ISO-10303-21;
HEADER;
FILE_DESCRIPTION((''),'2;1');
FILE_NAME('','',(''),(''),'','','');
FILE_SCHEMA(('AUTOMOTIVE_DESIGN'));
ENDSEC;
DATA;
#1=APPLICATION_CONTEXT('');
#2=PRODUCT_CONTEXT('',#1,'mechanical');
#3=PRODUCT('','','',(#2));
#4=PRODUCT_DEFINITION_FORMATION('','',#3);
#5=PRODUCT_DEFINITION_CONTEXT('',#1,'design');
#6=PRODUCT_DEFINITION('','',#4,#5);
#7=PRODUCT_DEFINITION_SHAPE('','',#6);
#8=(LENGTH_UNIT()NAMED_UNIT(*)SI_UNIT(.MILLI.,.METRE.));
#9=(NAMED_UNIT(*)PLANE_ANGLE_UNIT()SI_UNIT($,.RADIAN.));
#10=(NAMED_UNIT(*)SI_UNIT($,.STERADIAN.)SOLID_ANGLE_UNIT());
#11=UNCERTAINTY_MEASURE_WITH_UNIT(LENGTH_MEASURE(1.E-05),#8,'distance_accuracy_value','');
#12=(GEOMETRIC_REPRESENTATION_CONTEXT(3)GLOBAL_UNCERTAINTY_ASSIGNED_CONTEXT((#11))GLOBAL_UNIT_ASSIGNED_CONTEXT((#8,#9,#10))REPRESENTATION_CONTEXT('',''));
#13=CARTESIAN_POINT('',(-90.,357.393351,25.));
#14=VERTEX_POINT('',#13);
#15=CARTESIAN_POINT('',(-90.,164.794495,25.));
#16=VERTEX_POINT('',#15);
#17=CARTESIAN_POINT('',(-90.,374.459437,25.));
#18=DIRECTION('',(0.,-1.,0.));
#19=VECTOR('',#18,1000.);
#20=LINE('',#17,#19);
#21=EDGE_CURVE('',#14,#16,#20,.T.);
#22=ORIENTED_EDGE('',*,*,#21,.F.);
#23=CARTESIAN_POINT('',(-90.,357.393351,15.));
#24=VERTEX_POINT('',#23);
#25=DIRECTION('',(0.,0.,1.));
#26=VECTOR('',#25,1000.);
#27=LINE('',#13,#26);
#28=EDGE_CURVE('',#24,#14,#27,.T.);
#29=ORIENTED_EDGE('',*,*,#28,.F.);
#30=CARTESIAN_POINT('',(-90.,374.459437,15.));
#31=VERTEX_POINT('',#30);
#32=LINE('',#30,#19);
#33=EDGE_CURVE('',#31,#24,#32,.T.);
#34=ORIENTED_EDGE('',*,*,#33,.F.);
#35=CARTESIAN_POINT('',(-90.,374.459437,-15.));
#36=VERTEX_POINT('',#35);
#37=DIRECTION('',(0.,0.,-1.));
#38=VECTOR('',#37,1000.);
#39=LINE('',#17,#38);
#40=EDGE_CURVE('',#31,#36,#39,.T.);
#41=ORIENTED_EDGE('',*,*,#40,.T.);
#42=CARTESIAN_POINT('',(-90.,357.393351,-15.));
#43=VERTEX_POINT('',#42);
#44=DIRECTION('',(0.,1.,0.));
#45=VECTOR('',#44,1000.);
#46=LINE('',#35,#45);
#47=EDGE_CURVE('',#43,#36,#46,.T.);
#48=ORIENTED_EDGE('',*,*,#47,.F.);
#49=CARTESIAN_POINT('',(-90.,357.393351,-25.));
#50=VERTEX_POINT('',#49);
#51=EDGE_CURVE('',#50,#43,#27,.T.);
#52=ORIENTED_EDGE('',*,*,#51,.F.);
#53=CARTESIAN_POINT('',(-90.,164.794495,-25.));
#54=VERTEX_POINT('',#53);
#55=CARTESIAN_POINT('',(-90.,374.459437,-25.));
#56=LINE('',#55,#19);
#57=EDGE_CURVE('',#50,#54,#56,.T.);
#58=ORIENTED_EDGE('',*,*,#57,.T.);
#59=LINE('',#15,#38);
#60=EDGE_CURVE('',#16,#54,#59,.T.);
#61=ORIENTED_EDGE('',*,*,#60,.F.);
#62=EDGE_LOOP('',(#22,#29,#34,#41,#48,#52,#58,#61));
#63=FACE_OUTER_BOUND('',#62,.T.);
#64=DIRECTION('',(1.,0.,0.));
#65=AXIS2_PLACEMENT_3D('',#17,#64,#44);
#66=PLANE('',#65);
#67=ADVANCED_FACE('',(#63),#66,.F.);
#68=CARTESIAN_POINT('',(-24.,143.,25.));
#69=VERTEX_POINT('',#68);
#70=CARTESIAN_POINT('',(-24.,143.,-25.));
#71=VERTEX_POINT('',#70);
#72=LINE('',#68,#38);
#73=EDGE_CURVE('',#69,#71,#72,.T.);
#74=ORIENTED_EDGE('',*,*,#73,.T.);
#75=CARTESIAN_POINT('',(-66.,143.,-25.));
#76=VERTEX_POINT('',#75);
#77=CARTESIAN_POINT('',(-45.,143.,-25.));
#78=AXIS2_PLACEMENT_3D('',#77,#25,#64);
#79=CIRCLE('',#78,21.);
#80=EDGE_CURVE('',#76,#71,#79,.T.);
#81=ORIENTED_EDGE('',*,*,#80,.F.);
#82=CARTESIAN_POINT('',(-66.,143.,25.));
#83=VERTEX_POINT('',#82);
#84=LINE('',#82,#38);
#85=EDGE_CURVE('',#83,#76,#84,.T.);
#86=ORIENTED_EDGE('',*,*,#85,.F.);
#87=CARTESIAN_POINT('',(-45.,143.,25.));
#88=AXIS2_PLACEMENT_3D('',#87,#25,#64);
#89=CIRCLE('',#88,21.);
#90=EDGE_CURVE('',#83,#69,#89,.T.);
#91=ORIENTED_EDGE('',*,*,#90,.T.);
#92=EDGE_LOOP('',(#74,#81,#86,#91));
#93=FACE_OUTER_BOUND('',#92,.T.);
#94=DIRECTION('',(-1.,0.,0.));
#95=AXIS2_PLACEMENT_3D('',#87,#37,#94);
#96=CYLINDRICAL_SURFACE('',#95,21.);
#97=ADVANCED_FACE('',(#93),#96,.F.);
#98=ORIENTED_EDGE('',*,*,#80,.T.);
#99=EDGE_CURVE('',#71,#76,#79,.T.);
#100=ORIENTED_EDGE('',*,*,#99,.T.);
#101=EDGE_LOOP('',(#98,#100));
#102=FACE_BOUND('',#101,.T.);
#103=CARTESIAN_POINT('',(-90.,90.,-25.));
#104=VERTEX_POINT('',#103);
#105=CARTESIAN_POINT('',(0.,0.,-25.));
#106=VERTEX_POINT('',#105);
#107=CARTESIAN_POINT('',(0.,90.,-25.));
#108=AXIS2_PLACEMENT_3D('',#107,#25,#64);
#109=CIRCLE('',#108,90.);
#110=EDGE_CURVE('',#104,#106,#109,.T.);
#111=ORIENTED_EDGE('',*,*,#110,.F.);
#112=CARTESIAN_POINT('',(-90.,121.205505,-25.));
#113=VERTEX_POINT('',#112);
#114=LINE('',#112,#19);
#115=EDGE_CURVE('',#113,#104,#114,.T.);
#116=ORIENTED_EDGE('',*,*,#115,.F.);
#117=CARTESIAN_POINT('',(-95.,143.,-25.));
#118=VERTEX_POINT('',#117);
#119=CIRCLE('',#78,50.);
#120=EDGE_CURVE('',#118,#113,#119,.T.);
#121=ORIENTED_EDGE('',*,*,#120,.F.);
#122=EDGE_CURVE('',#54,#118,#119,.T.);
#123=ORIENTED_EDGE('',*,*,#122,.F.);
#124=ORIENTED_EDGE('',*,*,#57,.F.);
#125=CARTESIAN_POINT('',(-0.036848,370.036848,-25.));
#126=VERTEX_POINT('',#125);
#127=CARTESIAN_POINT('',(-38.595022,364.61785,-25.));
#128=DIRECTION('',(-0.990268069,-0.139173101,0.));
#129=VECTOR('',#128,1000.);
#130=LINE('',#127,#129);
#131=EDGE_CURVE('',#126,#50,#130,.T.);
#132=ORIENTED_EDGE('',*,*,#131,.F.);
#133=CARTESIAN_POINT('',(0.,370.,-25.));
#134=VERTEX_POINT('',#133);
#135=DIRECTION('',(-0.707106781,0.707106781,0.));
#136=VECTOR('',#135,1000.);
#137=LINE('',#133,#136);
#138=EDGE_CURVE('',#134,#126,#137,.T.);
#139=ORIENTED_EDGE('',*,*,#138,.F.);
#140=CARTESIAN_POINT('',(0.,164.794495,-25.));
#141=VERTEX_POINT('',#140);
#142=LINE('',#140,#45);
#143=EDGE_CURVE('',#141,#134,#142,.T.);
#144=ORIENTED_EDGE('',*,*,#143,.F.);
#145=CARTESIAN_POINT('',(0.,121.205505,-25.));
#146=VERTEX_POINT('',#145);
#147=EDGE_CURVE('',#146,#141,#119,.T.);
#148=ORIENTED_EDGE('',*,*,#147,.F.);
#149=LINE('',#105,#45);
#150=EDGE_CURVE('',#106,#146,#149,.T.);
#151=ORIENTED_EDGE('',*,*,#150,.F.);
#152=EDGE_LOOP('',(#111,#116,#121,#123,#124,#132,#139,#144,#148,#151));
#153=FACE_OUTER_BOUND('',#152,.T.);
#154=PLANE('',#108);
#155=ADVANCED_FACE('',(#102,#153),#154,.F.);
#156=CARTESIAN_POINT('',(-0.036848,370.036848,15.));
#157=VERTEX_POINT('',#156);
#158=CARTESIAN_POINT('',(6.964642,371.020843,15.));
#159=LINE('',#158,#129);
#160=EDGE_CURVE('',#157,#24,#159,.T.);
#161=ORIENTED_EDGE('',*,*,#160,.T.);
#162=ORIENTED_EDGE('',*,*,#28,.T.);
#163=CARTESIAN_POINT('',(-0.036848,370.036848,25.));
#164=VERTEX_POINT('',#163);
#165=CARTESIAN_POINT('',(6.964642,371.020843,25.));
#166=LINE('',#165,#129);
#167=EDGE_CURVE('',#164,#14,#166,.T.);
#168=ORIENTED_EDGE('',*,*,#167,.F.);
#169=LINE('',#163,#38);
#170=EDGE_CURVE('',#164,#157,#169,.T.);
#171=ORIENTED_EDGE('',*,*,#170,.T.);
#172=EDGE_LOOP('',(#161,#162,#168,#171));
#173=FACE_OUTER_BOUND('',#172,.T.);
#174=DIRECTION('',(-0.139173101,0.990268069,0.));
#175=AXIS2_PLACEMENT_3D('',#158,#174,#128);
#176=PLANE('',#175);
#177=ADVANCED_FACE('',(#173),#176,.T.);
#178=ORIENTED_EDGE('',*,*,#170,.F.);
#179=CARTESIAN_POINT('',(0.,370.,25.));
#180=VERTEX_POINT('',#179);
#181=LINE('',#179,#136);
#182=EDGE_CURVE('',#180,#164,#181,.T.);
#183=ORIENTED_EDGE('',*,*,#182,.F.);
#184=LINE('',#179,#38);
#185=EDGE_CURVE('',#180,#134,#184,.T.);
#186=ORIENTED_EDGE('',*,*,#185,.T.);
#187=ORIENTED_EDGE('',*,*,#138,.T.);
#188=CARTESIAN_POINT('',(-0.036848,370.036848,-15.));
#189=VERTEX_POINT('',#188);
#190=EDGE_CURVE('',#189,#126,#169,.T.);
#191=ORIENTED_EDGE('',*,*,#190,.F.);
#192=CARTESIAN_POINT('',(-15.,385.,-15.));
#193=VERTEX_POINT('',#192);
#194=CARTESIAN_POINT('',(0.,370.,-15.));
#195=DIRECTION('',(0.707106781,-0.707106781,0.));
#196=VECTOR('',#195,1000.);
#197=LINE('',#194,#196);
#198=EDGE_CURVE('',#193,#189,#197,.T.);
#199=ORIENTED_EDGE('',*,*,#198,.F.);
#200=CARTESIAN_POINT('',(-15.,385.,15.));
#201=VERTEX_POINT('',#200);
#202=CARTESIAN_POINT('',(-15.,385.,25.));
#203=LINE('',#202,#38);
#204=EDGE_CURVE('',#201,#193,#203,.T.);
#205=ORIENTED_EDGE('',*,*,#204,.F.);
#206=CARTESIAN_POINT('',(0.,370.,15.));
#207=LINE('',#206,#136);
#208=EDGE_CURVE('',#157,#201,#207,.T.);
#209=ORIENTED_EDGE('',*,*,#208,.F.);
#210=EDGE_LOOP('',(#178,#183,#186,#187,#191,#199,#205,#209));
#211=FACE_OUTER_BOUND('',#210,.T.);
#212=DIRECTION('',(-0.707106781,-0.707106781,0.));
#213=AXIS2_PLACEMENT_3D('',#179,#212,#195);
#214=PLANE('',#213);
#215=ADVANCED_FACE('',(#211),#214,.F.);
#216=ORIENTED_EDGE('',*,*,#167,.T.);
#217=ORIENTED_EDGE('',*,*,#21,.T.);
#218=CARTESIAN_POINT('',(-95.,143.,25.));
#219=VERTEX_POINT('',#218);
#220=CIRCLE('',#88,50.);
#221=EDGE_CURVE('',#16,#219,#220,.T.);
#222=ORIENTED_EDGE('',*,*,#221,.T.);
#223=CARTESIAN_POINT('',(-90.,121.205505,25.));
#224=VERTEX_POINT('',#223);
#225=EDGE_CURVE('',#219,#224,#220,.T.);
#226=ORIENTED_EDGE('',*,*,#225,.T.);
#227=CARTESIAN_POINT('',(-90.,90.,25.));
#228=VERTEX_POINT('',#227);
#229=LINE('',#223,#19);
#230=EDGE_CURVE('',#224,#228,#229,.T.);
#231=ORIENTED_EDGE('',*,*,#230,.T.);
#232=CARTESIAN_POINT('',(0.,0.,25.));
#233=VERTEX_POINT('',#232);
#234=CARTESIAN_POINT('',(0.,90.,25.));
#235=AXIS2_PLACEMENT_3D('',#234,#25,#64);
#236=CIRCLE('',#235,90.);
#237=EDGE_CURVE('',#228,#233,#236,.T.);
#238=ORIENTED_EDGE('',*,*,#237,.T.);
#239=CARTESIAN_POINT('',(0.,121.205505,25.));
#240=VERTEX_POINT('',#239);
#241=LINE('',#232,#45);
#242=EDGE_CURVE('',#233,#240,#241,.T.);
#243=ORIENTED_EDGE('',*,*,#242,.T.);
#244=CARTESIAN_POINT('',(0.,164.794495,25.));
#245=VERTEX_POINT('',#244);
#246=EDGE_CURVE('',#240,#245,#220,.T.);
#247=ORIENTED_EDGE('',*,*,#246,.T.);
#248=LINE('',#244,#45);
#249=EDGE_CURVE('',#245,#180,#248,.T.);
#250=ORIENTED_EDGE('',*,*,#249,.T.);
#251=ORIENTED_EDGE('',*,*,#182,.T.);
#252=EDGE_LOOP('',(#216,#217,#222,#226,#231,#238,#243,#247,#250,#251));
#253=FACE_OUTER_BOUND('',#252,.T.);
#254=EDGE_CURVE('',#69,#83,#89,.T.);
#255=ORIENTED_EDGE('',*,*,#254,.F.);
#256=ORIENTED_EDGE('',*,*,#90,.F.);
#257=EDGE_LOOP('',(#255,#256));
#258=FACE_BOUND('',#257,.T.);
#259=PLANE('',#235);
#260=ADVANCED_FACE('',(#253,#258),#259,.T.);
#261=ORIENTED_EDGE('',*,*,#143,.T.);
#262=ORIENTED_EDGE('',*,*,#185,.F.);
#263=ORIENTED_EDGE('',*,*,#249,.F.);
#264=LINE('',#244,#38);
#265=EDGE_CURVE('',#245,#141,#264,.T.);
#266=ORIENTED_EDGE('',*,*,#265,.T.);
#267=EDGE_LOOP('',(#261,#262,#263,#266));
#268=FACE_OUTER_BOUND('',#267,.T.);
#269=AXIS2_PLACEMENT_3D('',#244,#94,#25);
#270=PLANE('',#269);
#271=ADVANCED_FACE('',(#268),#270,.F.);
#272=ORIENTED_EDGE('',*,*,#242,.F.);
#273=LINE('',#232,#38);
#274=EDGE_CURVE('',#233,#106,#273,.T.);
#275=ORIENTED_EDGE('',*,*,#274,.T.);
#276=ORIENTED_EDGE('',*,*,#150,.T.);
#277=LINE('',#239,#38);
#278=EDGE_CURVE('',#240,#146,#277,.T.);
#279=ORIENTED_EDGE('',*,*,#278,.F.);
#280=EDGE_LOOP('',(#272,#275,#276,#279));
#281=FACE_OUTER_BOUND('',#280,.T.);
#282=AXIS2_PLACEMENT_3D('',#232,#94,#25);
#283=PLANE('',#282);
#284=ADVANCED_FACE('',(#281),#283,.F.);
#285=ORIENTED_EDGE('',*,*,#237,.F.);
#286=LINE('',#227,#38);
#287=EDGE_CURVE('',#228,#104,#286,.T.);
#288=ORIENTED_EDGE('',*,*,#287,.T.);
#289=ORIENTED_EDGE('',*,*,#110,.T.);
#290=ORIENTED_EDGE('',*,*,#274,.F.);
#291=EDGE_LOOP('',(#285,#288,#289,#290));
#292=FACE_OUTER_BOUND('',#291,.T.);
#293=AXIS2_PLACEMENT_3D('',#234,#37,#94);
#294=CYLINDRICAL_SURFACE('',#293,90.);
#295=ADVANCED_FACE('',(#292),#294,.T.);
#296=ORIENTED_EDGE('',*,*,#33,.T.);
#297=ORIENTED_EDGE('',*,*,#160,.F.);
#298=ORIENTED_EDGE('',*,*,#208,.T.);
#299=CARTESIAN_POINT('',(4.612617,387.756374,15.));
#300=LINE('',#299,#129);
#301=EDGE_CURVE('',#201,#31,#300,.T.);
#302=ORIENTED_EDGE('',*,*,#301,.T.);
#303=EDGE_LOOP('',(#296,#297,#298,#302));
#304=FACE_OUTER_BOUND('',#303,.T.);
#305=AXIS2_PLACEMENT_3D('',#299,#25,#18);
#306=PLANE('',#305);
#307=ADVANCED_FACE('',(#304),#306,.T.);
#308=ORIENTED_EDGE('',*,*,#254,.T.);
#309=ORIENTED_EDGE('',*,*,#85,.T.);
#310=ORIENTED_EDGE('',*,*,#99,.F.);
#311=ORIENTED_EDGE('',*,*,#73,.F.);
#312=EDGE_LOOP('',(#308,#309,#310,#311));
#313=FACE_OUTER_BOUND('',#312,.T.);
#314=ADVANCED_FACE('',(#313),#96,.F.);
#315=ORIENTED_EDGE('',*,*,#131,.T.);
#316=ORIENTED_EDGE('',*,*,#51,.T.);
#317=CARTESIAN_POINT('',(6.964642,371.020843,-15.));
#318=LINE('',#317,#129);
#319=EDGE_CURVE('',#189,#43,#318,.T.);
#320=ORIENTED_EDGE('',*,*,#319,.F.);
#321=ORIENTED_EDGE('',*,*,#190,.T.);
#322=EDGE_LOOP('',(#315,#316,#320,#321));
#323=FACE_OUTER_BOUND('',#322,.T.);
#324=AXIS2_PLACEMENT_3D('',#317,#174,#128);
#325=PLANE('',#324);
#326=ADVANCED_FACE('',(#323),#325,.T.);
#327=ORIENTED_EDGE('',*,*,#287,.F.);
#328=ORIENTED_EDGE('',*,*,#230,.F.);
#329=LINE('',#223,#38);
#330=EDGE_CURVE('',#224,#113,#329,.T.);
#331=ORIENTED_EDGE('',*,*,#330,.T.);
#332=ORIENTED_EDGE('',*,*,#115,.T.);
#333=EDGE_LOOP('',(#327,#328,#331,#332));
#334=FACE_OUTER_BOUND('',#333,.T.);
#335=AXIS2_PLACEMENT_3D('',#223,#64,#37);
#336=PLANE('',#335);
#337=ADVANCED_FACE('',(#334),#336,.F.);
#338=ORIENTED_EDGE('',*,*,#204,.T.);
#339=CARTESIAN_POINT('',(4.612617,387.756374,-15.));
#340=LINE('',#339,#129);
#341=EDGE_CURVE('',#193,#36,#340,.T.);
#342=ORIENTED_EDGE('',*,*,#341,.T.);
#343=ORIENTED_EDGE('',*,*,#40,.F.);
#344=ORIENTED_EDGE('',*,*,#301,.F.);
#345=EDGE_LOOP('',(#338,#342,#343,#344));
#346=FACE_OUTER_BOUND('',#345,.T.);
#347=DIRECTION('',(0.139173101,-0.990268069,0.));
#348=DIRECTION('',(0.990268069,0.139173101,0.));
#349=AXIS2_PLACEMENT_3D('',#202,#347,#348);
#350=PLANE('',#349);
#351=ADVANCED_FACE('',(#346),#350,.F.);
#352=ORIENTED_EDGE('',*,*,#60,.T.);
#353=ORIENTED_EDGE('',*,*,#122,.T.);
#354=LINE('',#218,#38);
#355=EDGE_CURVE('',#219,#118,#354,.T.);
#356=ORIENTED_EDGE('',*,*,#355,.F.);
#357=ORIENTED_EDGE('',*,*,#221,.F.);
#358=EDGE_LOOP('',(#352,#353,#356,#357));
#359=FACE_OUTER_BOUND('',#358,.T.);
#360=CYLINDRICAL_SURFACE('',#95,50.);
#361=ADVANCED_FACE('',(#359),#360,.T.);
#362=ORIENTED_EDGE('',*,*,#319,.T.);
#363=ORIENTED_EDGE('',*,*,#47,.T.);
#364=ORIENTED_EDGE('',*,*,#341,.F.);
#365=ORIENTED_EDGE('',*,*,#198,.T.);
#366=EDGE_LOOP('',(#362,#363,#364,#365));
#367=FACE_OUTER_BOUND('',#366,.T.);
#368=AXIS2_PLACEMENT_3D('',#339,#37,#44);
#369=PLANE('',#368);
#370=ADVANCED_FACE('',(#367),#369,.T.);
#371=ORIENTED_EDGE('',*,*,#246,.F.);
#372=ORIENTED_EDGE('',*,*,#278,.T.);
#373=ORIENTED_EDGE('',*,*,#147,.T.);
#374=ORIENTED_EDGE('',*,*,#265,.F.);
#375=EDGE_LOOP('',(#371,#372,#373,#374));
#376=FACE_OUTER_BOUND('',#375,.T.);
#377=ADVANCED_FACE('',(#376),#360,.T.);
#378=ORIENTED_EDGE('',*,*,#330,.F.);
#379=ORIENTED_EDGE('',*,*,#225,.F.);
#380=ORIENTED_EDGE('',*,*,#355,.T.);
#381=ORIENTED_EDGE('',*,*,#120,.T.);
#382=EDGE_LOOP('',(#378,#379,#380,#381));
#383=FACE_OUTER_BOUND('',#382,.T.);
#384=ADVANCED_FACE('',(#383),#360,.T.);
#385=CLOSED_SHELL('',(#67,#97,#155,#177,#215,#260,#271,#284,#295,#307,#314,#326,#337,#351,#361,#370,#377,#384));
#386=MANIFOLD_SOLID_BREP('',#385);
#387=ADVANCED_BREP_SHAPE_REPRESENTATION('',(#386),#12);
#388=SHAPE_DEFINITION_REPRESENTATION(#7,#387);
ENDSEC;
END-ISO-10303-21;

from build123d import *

# Parameters (mm, degrees)
SKETCH_1_R               = 21
EXTRUDE_1_DEPTH          = 25
CUT_EXTRUDE_1_DEPTH      = 396.281407624
CUT_EXTRUDE_1_DEPTH_BACK = 396.281407624
SKETCH_2_W               = 10
SKETCH_2_H               = 16.9


with BuildPart() as part:
    # 草图1 → 凸台-拉伸1 (new, symmetric)
    with BuildSketch(Plane.XY):
        with BuildLine():
            Line((0, 0), (0, 121.205505282))
            ThreePointArc((0, 121.205505282), (5, 143), (0, 164.794494718))
            Line((0, 164.794494718), (0, 370))
            Line((0, 370), (-15, 385))
            Line((-15, 385), (-90, 374.459437397))
            Line((-90, 374.459437397), (-90, 164.794494718))
            ThreePointArc((-90, 164.794494718), (-95, 143), (-90, 121.205505282))
            Line((-90, 121.205505282), (-90, 90))
            ThreePointArc((-90, 90), (-63.639610307, 26.360389693), (0, 0))
        make_face()
        with Locations((-45, 143)):
            Circle(SKETCH_1_R, mode=Mode.SUBTRACT)
    extrude(amount=EXTRUDE_1_DEPTH, both=True)

    # 草图2 → 切除-拉伸1 (cut, two sides: drawn at the far end of the back side and taken through both)
    with BuildSketch(Plane(origin=(-36.649271725, -5.150719239, 0), x_dir=(0, 0, -1), z_dir=(0.9902680687415697, 0.1391731009600695, 0)).offset(-CUT_EXTRUDE_1_DEPTH_BACK)):
        with Locations((-20, 374.89080298)):
            Rectangle(SKETCH_2_W, SKETCH_2_H)
        with Locations((20, 374.89080298)):
            Rectangle(SKETCH_2_W, SKETCH_2_H)
    extrude(amount=CUT_EXTRUDE_1_DEPTH + CUT_EXTRUDE_1_DEPTH_BACK, mode=Mode.SUBTRACT)


solid = part.part
